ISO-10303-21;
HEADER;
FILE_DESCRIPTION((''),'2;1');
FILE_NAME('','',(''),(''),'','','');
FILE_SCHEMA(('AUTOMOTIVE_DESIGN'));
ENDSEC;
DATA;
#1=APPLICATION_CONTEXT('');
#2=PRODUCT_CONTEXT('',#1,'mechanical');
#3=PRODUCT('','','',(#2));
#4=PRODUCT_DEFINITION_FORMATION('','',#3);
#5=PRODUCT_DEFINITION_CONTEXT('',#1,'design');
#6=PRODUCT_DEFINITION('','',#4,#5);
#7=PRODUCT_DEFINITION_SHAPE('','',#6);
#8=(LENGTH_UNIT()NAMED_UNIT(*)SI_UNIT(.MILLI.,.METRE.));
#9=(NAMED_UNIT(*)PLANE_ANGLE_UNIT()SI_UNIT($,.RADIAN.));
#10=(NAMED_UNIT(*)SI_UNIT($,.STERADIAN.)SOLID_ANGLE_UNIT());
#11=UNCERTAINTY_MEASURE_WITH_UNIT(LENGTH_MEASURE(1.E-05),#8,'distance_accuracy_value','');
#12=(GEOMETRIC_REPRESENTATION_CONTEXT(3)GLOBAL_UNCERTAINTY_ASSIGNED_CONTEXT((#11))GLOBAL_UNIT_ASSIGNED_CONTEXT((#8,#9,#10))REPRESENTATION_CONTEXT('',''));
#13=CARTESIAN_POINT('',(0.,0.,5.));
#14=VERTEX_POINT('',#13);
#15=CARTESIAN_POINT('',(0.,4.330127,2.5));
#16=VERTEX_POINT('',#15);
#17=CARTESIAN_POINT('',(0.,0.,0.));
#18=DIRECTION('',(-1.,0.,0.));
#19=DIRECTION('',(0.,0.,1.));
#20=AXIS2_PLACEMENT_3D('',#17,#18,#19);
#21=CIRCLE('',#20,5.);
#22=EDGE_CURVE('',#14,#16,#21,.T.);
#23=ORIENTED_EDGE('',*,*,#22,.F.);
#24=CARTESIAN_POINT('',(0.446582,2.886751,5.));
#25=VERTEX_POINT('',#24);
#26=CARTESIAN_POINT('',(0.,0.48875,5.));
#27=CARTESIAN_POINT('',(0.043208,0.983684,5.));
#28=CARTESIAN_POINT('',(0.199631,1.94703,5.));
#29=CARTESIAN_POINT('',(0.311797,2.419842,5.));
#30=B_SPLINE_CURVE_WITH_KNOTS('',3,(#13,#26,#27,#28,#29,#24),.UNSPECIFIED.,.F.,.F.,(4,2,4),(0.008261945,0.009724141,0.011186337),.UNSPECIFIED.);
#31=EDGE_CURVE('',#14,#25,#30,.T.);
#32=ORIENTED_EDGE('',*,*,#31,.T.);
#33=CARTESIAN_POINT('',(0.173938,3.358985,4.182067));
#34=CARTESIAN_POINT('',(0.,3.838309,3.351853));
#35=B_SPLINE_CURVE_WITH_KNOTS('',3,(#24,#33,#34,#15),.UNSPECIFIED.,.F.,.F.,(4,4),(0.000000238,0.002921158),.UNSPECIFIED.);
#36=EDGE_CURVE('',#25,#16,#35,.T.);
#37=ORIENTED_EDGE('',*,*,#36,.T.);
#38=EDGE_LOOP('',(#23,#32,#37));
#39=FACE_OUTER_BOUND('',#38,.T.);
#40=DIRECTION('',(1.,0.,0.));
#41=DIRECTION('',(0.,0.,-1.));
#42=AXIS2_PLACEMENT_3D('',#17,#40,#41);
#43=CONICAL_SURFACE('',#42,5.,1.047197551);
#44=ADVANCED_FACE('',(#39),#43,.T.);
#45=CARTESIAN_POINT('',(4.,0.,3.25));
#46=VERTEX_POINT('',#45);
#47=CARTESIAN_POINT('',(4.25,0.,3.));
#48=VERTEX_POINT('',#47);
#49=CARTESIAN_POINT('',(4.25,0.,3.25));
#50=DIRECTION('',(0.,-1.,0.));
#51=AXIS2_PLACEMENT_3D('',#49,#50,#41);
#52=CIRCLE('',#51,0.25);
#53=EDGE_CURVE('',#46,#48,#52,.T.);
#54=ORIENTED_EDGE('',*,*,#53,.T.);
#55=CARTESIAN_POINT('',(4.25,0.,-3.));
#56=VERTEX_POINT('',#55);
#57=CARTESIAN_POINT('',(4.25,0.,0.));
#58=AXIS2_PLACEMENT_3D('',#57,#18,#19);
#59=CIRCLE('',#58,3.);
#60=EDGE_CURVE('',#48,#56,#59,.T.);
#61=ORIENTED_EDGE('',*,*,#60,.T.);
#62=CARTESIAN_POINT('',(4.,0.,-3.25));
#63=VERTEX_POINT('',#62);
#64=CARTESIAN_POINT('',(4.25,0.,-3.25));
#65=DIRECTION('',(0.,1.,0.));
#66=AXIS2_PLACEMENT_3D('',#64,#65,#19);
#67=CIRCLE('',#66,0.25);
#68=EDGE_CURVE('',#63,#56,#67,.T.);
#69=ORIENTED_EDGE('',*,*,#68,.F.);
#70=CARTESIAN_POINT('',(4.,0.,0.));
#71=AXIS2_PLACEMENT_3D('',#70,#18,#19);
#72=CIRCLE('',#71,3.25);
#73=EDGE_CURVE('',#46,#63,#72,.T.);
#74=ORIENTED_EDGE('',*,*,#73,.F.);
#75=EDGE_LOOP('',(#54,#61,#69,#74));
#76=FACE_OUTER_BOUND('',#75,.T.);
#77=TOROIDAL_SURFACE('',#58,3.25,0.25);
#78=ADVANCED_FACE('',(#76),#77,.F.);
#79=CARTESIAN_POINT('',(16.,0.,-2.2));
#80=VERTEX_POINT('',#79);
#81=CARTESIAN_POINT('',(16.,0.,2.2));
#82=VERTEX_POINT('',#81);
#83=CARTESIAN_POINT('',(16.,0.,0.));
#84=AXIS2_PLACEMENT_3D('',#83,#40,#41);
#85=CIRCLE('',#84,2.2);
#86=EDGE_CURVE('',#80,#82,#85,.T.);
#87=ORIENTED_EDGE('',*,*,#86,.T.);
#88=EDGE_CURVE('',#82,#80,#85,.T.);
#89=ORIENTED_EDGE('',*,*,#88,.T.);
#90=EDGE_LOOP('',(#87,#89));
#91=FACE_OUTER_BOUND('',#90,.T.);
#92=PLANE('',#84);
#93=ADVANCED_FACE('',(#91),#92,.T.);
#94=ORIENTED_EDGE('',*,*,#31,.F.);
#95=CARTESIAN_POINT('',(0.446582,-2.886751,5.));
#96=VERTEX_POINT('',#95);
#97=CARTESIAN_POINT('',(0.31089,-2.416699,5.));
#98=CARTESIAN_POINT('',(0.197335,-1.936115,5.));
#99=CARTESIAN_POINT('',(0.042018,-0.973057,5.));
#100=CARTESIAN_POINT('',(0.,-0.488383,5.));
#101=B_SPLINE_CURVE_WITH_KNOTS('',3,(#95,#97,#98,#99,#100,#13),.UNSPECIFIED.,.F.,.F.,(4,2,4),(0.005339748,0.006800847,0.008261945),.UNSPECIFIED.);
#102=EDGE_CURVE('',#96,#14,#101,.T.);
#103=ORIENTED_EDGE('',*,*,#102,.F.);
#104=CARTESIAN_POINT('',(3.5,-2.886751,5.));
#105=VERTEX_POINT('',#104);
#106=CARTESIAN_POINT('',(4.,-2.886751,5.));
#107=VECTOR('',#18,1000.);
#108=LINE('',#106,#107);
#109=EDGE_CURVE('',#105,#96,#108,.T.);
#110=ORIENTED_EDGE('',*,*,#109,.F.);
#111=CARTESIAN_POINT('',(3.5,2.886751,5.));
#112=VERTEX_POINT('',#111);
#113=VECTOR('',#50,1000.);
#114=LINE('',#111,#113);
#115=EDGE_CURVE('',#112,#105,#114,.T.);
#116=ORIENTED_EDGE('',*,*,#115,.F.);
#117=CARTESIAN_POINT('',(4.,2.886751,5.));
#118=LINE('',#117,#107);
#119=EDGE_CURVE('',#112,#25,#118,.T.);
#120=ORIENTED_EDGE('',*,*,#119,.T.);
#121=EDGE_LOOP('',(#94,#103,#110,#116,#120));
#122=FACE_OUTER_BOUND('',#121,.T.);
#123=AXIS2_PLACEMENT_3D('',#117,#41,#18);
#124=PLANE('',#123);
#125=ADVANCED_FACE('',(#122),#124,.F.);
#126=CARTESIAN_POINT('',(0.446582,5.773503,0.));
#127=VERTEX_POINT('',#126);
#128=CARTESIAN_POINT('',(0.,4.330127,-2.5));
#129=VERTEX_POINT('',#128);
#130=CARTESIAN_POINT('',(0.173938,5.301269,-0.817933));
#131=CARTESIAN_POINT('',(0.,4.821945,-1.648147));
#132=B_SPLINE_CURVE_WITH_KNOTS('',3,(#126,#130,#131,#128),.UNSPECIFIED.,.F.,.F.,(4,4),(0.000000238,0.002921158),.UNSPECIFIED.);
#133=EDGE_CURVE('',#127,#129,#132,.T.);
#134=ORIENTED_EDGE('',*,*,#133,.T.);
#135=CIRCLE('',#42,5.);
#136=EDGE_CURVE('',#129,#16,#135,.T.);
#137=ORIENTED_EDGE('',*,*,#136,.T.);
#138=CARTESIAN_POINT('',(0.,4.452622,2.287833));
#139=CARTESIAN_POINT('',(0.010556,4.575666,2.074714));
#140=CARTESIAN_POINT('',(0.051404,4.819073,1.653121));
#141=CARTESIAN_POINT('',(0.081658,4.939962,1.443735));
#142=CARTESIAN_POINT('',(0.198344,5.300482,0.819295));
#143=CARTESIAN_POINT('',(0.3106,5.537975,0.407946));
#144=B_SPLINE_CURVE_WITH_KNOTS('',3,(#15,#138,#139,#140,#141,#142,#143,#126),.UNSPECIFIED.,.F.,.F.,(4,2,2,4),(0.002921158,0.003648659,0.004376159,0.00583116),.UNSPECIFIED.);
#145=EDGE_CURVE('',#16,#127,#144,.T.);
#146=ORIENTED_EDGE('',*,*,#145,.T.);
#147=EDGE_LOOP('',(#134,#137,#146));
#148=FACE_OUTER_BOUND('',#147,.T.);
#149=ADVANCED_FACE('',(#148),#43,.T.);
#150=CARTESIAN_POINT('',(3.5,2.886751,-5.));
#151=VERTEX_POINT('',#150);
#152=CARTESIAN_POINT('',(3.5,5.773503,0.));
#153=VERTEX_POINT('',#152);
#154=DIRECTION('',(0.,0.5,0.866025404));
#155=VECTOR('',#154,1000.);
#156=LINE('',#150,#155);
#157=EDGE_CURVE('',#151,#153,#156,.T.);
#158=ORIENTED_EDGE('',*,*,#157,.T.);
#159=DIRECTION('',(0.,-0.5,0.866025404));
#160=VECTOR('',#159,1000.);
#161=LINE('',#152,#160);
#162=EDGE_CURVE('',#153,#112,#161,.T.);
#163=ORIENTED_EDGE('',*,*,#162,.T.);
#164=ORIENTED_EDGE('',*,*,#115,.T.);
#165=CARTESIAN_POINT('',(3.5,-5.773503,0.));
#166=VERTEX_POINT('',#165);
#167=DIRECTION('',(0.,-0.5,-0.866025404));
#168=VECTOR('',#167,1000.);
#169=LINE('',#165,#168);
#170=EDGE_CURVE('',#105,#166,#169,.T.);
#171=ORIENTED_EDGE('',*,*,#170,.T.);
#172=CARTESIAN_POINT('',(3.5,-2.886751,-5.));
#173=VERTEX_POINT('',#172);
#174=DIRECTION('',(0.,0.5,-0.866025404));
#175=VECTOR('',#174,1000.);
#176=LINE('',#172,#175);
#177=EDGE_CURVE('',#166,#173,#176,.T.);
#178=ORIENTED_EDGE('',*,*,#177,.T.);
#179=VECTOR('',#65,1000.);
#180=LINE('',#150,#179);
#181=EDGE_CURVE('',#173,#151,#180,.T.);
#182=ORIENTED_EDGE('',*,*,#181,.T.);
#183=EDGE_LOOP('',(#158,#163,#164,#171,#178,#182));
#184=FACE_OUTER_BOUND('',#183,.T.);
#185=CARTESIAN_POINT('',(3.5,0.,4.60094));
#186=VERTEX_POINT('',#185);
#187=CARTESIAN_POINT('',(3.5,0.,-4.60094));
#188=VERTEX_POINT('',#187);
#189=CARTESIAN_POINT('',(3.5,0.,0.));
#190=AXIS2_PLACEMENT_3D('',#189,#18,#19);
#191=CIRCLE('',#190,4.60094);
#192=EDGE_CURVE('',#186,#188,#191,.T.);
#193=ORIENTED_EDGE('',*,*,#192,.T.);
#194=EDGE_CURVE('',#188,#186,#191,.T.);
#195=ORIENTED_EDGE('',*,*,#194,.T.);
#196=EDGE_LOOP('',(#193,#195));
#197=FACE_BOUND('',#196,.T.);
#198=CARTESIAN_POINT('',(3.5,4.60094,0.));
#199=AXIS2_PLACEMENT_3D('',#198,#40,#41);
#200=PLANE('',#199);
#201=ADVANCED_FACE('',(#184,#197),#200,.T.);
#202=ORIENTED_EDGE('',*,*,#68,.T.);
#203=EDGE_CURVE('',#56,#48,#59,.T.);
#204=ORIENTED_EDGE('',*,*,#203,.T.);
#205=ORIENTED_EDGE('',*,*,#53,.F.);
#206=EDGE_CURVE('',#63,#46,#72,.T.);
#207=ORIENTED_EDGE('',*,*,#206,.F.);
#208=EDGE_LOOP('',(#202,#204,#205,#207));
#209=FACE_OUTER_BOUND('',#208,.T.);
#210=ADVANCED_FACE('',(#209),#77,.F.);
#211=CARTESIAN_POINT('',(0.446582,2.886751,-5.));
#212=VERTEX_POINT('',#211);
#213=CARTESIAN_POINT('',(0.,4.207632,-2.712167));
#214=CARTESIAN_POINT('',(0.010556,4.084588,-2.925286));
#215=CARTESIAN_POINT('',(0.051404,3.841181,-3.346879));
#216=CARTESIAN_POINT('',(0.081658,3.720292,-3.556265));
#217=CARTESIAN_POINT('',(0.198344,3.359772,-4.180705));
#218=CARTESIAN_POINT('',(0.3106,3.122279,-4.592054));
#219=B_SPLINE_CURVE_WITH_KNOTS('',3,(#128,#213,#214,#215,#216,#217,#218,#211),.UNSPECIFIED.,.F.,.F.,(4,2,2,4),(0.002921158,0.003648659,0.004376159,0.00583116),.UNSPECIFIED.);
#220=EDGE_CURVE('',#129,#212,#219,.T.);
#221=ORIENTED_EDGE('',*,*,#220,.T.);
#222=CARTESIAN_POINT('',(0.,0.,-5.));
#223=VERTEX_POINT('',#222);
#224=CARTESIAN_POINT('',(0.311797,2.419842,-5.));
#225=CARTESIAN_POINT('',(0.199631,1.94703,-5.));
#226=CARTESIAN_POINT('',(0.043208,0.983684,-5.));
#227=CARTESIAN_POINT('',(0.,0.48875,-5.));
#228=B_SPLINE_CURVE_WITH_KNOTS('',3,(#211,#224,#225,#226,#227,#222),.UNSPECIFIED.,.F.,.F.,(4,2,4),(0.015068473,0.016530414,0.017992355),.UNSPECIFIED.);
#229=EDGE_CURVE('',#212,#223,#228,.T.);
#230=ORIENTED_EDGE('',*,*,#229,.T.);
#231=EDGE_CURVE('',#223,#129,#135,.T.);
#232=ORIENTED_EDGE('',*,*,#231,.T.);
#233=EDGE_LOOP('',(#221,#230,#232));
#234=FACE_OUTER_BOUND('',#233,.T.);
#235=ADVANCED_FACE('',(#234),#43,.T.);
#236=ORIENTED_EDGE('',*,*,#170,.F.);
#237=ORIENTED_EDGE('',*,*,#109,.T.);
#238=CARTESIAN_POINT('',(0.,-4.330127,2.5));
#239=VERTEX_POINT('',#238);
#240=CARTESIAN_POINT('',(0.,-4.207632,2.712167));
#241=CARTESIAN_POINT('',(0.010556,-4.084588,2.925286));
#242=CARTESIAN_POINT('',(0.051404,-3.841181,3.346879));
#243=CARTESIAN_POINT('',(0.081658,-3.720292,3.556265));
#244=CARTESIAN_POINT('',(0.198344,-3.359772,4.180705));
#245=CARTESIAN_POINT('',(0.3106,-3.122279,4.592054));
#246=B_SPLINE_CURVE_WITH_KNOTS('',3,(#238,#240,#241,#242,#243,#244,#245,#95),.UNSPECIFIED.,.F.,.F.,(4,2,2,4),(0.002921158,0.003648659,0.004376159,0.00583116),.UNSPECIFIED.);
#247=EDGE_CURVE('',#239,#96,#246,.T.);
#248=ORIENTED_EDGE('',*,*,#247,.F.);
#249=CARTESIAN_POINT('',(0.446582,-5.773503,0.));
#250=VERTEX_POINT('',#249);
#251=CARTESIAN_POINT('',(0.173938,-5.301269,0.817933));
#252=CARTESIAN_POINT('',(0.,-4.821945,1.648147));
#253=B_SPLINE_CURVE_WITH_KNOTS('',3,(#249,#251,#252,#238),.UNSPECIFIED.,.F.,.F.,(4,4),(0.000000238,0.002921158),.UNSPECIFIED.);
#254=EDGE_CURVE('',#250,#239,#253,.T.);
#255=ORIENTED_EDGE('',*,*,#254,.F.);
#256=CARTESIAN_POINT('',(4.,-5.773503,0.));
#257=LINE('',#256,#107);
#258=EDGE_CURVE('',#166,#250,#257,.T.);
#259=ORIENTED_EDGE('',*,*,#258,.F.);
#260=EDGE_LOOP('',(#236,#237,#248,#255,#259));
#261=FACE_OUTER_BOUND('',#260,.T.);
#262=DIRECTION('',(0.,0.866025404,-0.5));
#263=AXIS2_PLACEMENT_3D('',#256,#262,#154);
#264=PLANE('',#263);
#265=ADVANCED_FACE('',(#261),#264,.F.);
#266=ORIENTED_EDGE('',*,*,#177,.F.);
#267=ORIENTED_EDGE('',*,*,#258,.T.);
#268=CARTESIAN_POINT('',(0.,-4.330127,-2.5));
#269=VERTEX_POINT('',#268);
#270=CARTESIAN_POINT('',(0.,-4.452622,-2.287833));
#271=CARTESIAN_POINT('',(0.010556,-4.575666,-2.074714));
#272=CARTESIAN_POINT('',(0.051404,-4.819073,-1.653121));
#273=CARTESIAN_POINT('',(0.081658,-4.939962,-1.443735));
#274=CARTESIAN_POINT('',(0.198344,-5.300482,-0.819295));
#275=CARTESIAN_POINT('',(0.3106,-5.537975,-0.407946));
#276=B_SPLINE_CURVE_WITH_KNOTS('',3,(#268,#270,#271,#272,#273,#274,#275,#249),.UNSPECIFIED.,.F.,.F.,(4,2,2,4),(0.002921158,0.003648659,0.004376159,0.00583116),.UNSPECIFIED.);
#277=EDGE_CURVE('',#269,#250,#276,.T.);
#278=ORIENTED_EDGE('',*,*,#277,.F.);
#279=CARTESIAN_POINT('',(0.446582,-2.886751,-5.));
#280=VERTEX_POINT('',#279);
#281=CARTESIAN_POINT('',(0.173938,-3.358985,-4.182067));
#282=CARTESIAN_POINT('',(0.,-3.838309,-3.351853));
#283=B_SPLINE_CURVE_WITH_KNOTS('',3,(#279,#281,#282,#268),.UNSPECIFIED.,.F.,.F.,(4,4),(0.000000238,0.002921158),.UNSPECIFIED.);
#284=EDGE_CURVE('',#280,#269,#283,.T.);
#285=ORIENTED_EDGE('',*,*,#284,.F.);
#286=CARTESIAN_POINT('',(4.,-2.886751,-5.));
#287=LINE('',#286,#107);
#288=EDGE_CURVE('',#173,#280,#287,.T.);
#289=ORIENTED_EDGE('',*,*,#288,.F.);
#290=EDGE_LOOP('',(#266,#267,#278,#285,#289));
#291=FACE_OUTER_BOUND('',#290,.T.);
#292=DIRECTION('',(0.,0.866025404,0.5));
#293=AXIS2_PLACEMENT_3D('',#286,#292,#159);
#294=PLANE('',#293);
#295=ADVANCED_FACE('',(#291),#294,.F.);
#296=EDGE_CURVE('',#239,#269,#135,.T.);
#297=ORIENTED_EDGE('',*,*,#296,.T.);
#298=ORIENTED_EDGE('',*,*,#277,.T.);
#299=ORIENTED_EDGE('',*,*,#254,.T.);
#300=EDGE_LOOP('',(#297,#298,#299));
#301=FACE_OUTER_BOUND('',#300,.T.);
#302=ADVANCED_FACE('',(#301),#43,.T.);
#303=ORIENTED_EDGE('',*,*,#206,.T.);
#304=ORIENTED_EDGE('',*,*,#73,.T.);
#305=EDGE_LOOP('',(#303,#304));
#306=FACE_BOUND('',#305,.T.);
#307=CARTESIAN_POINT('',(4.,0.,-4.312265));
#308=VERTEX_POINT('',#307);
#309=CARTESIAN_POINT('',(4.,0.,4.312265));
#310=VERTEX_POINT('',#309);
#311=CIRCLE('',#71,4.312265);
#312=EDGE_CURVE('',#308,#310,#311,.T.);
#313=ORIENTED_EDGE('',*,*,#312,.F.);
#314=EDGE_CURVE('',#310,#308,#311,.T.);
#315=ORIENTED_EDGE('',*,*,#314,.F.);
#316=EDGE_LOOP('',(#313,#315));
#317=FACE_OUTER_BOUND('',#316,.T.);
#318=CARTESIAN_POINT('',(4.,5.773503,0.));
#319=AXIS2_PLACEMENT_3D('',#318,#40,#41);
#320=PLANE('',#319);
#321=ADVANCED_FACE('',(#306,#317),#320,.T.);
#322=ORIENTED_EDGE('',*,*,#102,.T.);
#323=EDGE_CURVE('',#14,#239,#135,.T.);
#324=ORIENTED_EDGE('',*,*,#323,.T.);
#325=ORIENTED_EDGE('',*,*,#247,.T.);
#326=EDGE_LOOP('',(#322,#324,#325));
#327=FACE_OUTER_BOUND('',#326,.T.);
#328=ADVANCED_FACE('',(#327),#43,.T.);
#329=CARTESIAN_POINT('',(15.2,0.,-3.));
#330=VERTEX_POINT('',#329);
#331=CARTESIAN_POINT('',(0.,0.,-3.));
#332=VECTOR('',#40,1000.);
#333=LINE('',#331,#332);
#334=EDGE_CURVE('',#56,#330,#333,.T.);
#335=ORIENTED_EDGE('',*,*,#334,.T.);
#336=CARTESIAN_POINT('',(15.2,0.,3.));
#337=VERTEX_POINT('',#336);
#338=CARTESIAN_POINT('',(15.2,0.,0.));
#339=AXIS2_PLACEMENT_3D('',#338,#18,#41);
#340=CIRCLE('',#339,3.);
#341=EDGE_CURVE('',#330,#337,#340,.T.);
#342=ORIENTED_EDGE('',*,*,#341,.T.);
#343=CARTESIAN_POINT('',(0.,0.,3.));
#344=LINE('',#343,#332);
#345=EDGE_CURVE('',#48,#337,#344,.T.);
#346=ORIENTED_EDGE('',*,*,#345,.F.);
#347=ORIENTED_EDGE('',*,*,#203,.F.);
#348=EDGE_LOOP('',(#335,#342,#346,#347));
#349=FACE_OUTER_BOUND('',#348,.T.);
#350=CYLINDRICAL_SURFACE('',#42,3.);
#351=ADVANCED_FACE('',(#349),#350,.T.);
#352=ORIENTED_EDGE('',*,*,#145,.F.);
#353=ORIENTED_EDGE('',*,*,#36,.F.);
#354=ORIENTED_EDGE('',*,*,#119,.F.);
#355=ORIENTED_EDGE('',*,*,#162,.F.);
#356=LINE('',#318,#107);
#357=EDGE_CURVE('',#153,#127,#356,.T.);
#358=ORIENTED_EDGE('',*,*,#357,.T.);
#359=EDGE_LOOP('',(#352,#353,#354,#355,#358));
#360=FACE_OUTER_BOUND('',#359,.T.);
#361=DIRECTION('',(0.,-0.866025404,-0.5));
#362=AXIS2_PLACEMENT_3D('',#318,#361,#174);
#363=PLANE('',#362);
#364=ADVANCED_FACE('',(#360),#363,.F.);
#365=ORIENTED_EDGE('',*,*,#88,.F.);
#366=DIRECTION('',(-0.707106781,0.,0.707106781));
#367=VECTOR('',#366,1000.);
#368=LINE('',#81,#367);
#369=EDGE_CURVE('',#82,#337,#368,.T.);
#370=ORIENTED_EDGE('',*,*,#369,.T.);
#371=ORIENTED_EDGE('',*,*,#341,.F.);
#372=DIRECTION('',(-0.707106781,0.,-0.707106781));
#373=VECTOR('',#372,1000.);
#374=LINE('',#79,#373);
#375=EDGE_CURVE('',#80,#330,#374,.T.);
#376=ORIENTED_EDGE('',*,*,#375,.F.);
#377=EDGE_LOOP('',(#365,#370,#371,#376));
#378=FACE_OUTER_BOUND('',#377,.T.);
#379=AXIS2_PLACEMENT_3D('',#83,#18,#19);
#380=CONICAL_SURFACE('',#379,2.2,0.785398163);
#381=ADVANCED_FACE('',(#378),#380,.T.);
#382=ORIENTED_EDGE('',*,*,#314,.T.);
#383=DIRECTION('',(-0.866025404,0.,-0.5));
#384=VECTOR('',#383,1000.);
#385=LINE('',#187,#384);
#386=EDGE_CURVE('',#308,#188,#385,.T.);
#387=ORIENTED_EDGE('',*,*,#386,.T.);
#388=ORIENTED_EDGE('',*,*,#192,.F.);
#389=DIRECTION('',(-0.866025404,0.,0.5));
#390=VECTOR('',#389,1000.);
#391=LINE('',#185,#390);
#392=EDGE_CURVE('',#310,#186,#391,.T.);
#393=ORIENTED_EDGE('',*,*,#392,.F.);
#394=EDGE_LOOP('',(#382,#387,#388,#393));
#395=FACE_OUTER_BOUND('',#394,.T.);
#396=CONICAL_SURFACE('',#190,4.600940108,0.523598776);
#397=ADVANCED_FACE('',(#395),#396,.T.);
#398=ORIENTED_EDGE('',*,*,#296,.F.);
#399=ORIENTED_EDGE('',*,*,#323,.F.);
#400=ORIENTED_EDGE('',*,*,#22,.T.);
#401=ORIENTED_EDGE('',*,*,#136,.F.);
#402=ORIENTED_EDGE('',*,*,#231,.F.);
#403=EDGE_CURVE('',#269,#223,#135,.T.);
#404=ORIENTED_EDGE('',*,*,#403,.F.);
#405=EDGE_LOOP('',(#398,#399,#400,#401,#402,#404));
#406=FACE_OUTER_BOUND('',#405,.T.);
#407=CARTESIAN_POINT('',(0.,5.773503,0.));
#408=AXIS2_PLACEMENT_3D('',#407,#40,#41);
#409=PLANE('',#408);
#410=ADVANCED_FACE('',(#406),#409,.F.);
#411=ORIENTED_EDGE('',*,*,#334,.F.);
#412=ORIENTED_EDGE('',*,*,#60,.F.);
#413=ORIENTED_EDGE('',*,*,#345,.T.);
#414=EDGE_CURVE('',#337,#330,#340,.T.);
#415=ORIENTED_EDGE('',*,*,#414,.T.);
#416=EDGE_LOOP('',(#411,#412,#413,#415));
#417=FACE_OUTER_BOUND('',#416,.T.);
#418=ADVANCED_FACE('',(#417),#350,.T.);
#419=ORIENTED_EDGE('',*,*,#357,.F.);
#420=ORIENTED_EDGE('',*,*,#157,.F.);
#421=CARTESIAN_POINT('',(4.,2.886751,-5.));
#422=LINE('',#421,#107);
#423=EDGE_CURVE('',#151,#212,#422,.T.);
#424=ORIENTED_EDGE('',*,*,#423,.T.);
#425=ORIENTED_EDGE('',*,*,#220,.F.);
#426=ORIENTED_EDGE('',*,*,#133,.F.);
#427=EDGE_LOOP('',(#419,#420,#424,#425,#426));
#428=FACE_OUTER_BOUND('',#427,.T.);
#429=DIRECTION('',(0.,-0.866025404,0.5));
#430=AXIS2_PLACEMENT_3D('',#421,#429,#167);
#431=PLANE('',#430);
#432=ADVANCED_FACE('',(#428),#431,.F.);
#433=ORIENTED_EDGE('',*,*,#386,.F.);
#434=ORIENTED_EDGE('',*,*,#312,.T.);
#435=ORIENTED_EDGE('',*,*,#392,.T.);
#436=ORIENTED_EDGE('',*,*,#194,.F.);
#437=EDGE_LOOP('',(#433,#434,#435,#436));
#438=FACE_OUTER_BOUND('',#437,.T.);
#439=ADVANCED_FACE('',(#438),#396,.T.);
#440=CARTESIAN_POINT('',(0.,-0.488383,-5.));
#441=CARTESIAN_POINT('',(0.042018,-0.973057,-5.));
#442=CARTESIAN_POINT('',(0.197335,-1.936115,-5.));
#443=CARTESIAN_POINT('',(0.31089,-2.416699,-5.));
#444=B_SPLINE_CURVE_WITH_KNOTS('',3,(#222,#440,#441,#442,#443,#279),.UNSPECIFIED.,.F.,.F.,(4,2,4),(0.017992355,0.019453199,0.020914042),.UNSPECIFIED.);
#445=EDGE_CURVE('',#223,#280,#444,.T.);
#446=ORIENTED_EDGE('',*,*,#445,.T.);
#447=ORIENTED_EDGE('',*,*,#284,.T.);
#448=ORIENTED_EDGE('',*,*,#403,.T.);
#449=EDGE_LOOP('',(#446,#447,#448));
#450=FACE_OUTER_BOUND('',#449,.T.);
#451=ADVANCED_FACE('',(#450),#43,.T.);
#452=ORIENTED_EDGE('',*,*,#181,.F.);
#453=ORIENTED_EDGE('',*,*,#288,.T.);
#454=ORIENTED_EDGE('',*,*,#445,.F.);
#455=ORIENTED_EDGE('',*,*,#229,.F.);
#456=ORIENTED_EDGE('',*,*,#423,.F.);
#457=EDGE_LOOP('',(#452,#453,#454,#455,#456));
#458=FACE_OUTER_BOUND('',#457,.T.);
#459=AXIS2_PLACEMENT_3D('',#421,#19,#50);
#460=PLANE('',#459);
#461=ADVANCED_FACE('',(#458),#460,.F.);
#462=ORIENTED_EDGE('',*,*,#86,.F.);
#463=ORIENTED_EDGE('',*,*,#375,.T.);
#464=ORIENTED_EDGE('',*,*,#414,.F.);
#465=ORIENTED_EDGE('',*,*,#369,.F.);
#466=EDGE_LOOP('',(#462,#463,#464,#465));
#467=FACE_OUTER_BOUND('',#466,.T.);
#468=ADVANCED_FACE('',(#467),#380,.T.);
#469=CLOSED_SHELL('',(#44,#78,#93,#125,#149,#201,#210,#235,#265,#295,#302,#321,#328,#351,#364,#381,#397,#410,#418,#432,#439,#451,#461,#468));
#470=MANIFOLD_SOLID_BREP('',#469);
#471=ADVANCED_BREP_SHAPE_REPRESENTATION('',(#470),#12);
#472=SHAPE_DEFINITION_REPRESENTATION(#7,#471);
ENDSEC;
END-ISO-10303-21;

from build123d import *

# Parameters (mm, degrees)
BASE_EXTRUDE_DEPTH = 4
CHAMFER_2_SIZE     = 0.8


with BuildPart() as part:
    # Sketch1 → Base-extrude (new body)
    with BuildSketch(Plane(origin=(0, 0, 0), x_dir=(0, 0, -1), z_dir=(1, 0, 0))):
        Polygon((5, 2.886751346), (5, -2.886751346), (0, -5.773502692), (-5, -2.886751346), (-5, 2.886751346), (0, 5.773502692), align=None)
    extrude(amount=BASE_EXTRUDE_DEPTH)

    # Sketch2 → Boss-Revolve1 (revolve)
    with BuildSketch(Plane.XY, mode=Mode.PRIVATE) as boss_revolve1_sk:
        Polygon((0, 0), (16, 0), (16, 2.134), (16, 3), (4, 3), (0, 3), align=None)
    revolve(boss_revolve1_sk.sketch.rotate(Axis((0, 0, 0), (-1, 0, 0)), 90), axis=Axis((0, 0, 0), (-1, 0, 0)))

    # Sketch3 → Cut-Revolve1 (revolve, cut)
    with BuildSketch(Plane.XY):
        Polygon((0, 5), (3.333333333, 10.773502692), (3.333333333, 15.773502692), (-10, 15.773502692), (-10, 5), align=None)
    revolve(axis=Axis((0, 0, 0), (1, 0, 0)), mode=Mode.SUBTRACT)

    # Sketch5 → Cut-Revolve2 (revolve, cut)
    with BuildSketch(Plane.XY):
        Polygon((4, 5), (0.666666667, 10.773502692), (0.666666667, 15.773502692), (10.666666667, 15.773502692), (10.666666667, 5), align=None)
    revolve(axis=Axis((0, 0, 0), (1, 0, 0)), mode=Mode.SUBTRACT)

    # Sketch4 → Cut-Revolve3 (revolve, cut)
    with BuildSketch(Plane.XY, mode=Mode.PRIVATE) as cut_revolve3_sk:
        Polygon((4, 4.312264973), (3.5, 4.600940108), (3.5, 15.773502692), (4, 15.773502692), align=None)
    revolve(cut_revolve3_sk.sketch.rotate(Axis((0, 0, 0), (1, 0, 0)), 90), axis=Axis((0, 0, 0), (1, 0, 0)), mode=Mode.SUBTRACT)

    # Chamfer 2
    chamfer_2_edges = [part.edges().sort_by_distance(p)[0] for p in [
        (16, 0, 3),
    ]]
    chamfer(chamfer_2_edges, length=CHAMFER_2_SIZE)

    # Sketch9 → Revolve1 (revolve)
    with BuildSketch(Plane.XY, mode=Mode.PRIVATE) as revolve1_sk:
        with BuildLine():
            Line((4, 3.25), (4, 3))
            Line((4, 3), (4.25, 3))
            ThreePointArc((4.25, 3), (4.073223305, 3.073223305), (4, 3.25))
        make_face()
    revolve(revolve1_sk.sketch.rotate(Axis((0, 0, 0), (1, 0, 0)), 90), axis=Axis((0, 0, 0), (1, 0, 0)))


solid = part.part
